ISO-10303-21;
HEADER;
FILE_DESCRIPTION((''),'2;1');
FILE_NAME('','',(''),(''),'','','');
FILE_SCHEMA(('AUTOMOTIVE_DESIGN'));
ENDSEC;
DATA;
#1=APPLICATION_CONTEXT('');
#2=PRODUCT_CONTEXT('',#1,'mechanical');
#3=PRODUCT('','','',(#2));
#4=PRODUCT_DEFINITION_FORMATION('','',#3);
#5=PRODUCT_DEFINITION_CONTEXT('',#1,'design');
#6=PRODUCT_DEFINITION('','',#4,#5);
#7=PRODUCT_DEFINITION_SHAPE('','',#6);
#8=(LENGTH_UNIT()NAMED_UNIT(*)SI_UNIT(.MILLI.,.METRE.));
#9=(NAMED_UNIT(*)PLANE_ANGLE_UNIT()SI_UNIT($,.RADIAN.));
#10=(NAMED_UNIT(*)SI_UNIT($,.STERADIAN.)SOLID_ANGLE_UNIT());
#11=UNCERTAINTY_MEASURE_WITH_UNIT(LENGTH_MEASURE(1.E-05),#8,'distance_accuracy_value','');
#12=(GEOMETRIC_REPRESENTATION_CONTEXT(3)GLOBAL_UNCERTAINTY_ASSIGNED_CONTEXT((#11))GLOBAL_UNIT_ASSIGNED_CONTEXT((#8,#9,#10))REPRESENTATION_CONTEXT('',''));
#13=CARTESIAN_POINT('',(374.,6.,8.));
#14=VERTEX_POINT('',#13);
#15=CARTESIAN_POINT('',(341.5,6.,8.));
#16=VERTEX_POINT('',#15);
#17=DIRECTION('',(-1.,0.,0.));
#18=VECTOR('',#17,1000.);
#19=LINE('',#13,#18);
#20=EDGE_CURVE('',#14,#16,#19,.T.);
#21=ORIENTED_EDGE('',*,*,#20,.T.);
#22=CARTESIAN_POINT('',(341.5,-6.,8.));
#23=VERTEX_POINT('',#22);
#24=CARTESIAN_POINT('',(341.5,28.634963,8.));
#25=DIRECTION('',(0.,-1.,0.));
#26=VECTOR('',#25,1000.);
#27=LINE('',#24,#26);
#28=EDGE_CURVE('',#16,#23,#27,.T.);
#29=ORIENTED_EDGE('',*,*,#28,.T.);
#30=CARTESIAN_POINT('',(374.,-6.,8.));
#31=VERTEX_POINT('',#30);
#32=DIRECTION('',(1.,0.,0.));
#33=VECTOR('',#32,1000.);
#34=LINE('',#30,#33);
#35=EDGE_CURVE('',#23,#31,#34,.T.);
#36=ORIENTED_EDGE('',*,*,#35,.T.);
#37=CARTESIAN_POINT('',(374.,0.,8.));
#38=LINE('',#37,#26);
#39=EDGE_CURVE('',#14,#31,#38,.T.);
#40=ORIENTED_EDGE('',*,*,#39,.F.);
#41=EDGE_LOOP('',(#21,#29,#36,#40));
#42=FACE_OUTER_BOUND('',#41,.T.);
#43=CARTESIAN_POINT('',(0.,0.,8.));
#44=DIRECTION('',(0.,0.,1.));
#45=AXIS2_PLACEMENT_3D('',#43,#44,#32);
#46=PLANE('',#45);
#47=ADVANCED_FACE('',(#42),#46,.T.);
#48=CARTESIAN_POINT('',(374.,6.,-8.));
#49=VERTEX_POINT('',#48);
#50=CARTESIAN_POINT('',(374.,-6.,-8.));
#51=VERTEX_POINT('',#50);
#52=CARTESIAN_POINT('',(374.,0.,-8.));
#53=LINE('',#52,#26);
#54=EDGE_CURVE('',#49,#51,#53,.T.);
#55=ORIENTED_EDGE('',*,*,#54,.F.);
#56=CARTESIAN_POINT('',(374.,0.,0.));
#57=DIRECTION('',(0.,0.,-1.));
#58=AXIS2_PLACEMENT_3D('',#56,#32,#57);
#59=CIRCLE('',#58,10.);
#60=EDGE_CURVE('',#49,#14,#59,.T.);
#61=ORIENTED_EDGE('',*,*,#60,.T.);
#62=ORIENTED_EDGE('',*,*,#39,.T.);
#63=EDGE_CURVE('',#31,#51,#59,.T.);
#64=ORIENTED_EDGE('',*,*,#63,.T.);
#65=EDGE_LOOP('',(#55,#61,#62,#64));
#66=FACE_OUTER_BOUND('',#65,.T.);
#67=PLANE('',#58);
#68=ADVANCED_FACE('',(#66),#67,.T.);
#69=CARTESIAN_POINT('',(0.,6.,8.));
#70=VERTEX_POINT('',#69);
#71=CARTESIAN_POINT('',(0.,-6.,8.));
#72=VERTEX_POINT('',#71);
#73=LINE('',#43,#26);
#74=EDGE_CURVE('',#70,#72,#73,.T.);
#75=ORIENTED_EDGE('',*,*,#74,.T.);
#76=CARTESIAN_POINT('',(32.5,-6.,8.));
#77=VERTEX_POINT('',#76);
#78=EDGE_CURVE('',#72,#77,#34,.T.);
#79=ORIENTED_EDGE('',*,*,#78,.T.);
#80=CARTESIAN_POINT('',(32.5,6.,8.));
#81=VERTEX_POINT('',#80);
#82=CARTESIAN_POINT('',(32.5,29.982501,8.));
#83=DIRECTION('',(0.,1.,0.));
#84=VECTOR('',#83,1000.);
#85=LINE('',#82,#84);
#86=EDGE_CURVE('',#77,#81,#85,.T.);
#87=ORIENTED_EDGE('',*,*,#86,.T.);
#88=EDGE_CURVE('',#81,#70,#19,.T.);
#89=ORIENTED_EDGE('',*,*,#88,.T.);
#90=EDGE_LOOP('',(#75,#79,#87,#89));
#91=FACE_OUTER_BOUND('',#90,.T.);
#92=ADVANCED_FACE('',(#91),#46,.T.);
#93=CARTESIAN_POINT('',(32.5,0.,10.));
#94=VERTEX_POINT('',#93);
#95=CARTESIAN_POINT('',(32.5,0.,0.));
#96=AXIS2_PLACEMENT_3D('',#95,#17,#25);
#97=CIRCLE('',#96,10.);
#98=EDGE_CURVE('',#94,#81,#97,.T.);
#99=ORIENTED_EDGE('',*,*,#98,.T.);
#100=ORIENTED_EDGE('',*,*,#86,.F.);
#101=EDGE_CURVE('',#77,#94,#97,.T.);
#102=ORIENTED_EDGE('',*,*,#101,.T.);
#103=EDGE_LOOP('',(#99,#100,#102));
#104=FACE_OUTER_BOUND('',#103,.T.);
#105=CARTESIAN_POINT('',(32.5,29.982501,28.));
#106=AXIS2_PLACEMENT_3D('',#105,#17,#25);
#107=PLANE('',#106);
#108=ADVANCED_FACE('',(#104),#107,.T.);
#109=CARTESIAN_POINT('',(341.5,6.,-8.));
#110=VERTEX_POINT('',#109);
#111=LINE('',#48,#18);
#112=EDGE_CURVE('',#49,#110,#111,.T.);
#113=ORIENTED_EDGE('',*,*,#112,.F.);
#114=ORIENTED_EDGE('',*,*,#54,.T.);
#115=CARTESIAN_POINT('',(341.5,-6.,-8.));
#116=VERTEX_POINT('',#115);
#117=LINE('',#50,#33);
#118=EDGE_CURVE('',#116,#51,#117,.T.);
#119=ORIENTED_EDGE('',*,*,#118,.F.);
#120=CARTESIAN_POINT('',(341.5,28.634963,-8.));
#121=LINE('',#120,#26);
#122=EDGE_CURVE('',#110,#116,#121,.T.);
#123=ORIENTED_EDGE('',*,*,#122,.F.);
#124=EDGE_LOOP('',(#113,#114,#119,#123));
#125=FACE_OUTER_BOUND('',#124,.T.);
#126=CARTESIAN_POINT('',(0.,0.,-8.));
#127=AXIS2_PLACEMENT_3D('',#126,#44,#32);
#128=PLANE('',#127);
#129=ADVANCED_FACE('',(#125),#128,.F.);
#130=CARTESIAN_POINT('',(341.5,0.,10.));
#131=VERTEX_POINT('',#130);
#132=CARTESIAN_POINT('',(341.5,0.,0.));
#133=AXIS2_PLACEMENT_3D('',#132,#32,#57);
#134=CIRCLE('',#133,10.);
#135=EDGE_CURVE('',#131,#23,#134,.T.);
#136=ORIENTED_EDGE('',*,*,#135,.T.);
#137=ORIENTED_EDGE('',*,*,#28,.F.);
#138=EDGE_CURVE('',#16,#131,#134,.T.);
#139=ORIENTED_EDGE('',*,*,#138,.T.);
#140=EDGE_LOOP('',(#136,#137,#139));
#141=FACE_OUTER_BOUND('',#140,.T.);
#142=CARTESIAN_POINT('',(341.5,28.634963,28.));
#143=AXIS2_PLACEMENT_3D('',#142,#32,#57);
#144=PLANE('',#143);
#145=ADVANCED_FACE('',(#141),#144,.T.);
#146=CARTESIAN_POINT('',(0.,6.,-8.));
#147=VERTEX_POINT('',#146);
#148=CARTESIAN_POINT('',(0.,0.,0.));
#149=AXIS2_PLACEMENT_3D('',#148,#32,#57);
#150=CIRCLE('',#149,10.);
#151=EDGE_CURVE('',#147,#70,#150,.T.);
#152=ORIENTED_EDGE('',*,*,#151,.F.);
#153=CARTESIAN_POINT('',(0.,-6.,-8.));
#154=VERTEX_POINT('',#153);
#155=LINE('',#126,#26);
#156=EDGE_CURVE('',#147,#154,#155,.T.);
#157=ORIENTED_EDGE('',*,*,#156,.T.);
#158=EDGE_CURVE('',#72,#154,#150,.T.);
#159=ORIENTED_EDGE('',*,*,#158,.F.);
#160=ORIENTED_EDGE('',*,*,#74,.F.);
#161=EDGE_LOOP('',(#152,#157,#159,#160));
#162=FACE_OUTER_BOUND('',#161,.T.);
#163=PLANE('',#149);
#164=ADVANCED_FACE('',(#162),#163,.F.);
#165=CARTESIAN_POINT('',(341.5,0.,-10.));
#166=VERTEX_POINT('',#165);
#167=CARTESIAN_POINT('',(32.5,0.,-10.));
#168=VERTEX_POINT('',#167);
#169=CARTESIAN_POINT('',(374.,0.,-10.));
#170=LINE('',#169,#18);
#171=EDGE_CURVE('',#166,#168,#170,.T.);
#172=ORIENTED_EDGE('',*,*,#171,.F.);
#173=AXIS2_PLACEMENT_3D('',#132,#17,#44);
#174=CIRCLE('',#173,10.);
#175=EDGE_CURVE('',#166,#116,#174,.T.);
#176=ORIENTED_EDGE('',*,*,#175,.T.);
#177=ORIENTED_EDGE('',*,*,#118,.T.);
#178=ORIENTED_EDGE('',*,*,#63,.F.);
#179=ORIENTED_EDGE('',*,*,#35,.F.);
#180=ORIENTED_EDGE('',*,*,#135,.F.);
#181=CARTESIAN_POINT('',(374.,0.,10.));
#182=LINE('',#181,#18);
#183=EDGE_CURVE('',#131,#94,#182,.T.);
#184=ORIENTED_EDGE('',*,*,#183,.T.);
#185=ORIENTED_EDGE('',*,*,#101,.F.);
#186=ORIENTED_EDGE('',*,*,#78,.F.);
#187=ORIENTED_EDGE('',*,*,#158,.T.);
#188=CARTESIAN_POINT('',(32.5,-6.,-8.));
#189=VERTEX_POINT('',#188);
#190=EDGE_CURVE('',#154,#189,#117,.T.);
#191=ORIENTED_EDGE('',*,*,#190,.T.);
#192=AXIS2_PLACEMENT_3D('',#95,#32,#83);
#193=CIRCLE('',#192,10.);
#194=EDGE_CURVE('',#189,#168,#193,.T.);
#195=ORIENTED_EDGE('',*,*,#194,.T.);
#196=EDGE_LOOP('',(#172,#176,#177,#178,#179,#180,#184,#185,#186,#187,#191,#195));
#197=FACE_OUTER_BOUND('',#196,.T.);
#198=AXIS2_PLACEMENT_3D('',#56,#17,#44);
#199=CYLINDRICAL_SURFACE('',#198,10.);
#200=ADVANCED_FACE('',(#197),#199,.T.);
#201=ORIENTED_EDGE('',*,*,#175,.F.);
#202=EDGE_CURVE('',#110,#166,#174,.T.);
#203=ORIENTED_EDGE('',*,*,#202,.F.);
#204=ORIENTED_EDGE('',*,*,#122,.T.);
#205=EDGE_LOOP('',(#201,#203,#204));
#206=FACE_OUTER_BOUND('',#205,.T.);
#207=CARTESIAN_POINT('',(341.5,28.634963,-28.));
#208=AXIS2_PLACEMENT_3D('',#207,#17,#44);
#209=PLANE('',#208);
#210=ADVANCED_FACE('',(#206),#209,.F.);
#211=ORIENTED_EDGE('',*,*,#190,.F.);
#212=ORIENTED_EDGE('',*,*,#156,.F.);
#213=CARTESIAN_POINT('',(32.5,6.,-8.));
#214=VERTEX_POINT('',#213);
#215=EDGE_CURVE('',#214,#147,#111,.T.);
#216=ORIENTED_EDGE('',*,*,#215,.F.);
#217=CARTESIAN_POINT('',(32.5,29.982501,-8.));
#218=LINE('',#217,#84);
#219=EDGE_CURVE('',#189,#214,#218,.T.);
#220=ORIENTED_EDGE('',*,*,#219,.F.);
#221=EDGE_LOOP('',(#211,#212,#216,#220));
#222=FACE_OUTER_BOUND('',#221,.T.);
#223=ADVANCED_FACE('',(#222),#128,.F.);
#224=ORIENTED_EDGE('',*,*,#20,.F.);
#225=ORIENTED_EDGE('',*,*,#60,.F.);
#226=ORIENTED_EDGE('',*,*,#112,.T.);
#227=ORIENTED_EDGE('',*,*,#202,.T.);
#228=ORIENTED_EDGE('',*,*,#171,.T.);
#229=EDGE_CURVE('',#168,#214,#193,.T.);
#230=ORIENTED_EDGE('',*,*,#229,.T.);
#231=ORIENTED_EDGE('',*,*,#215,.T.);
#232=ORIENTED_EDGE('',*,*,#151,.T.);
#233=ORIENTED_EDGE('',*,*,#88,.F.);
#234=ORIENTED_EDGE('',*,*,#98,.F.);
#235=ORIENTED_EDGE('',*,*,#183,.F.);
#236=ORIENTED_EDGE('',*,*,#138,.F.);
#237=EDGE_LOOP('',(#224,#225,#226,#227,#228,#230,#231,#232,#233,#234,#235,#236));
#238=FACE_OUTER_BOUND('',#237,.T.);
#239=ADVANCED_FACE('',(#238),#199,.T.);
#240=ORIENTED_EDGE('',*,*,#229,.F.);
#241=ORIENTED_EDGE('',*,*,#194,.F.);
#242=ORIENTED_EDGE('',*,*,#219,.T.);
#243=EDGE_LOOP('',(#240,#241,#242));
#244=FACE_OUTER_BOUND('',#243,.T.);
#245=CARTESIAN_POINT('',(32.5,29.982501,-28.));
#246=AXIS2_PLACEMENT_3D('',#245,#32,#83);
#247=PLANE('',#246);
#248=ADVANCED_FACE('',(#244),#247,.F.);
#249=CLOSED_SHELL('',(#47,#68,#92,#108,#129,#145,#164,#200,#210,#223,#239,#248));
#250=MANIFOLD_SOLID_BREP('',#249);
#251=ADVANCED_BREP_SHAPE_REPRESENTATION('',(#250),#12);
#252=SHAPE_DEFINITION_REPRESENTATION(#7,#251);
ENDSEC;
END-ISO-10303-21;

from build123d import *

# Parameters (mm, degrees)
SKETCH1_R           = 10
BOSS_EXTRUDE1_DEPTH = 374
CUT_EXTRUDE1_START  = -8
SKETCH_2_2_W        = 44.374102045
SKETCH_2_2_H        = 48.77153558
SKETCH_2_2_W_2      = 193.002207495
SKETCH_2_2_H_2      = 56.618631092
CUT_EXTRUDE1_DEPTH  = 20
CUT_EXTRUDE2_START  = 8
SKETCH_2_2_2_W      = 44.374102045
SKETCH_2_2_2_H      = 48.77153558
SKETCH_2_2_2_W_2    = 193.002207495
SKETCH_2_2_2_H_2    = 56.618631092
CUT_EXTRUDE2_DEPTH  = 20


with BuildPart() as part:
    # Sketch1 → Boss-Extrude1 (new body)
    with BuildSketch(Plane(origin=(0, 0, 0), x_dir=(0, 0, -1), z_dir=(1, 0, 0))):
        Circle(SKETCH1_R)
    extrude(amount=BOSS_EXTRUDE1_DEPTH)

    # Sketch 2_2 → Cut-Extrude1 (cut)
    with BuildSketch(Plane.XY.offset(CUT_EXTRUDE1_START)):
        with Locations((10.312948977, 5.596733591)):
            Rectangle(SKETCH_2_2_W, SKETCH_2_2_H)
        with Locations((438.001103747, 0.32564759)):
            Rectangle(SKETCH_2_2_W_2, SKETCH_2_2_H_2)
    extrude(amount=-CUT_EXTRUDE1_DEPTH, mode=Mode.SUBTRACT)

    # Sketch 2_2 2 → Cut-Extrude2 (cut)
    with BuildSketch(Plane.XY.offset(CUT_EXTRUDE2_START)):
        with Locations((10.312948977, 5.596733591)):
            Rectangle(SKETCH_2_2_2_W, SKETCH_2_2_2_H)
        with Locations((438.001103747, 0.32564759)):
            Rectangle(SKETCH_2_2_2_W_2, SKETCH_2_2_2_H_2)
    extrude(amount=CUT_EXTRUDE2_DEPTH, mode=Mode.SUBTRACT)


solid = part.part
